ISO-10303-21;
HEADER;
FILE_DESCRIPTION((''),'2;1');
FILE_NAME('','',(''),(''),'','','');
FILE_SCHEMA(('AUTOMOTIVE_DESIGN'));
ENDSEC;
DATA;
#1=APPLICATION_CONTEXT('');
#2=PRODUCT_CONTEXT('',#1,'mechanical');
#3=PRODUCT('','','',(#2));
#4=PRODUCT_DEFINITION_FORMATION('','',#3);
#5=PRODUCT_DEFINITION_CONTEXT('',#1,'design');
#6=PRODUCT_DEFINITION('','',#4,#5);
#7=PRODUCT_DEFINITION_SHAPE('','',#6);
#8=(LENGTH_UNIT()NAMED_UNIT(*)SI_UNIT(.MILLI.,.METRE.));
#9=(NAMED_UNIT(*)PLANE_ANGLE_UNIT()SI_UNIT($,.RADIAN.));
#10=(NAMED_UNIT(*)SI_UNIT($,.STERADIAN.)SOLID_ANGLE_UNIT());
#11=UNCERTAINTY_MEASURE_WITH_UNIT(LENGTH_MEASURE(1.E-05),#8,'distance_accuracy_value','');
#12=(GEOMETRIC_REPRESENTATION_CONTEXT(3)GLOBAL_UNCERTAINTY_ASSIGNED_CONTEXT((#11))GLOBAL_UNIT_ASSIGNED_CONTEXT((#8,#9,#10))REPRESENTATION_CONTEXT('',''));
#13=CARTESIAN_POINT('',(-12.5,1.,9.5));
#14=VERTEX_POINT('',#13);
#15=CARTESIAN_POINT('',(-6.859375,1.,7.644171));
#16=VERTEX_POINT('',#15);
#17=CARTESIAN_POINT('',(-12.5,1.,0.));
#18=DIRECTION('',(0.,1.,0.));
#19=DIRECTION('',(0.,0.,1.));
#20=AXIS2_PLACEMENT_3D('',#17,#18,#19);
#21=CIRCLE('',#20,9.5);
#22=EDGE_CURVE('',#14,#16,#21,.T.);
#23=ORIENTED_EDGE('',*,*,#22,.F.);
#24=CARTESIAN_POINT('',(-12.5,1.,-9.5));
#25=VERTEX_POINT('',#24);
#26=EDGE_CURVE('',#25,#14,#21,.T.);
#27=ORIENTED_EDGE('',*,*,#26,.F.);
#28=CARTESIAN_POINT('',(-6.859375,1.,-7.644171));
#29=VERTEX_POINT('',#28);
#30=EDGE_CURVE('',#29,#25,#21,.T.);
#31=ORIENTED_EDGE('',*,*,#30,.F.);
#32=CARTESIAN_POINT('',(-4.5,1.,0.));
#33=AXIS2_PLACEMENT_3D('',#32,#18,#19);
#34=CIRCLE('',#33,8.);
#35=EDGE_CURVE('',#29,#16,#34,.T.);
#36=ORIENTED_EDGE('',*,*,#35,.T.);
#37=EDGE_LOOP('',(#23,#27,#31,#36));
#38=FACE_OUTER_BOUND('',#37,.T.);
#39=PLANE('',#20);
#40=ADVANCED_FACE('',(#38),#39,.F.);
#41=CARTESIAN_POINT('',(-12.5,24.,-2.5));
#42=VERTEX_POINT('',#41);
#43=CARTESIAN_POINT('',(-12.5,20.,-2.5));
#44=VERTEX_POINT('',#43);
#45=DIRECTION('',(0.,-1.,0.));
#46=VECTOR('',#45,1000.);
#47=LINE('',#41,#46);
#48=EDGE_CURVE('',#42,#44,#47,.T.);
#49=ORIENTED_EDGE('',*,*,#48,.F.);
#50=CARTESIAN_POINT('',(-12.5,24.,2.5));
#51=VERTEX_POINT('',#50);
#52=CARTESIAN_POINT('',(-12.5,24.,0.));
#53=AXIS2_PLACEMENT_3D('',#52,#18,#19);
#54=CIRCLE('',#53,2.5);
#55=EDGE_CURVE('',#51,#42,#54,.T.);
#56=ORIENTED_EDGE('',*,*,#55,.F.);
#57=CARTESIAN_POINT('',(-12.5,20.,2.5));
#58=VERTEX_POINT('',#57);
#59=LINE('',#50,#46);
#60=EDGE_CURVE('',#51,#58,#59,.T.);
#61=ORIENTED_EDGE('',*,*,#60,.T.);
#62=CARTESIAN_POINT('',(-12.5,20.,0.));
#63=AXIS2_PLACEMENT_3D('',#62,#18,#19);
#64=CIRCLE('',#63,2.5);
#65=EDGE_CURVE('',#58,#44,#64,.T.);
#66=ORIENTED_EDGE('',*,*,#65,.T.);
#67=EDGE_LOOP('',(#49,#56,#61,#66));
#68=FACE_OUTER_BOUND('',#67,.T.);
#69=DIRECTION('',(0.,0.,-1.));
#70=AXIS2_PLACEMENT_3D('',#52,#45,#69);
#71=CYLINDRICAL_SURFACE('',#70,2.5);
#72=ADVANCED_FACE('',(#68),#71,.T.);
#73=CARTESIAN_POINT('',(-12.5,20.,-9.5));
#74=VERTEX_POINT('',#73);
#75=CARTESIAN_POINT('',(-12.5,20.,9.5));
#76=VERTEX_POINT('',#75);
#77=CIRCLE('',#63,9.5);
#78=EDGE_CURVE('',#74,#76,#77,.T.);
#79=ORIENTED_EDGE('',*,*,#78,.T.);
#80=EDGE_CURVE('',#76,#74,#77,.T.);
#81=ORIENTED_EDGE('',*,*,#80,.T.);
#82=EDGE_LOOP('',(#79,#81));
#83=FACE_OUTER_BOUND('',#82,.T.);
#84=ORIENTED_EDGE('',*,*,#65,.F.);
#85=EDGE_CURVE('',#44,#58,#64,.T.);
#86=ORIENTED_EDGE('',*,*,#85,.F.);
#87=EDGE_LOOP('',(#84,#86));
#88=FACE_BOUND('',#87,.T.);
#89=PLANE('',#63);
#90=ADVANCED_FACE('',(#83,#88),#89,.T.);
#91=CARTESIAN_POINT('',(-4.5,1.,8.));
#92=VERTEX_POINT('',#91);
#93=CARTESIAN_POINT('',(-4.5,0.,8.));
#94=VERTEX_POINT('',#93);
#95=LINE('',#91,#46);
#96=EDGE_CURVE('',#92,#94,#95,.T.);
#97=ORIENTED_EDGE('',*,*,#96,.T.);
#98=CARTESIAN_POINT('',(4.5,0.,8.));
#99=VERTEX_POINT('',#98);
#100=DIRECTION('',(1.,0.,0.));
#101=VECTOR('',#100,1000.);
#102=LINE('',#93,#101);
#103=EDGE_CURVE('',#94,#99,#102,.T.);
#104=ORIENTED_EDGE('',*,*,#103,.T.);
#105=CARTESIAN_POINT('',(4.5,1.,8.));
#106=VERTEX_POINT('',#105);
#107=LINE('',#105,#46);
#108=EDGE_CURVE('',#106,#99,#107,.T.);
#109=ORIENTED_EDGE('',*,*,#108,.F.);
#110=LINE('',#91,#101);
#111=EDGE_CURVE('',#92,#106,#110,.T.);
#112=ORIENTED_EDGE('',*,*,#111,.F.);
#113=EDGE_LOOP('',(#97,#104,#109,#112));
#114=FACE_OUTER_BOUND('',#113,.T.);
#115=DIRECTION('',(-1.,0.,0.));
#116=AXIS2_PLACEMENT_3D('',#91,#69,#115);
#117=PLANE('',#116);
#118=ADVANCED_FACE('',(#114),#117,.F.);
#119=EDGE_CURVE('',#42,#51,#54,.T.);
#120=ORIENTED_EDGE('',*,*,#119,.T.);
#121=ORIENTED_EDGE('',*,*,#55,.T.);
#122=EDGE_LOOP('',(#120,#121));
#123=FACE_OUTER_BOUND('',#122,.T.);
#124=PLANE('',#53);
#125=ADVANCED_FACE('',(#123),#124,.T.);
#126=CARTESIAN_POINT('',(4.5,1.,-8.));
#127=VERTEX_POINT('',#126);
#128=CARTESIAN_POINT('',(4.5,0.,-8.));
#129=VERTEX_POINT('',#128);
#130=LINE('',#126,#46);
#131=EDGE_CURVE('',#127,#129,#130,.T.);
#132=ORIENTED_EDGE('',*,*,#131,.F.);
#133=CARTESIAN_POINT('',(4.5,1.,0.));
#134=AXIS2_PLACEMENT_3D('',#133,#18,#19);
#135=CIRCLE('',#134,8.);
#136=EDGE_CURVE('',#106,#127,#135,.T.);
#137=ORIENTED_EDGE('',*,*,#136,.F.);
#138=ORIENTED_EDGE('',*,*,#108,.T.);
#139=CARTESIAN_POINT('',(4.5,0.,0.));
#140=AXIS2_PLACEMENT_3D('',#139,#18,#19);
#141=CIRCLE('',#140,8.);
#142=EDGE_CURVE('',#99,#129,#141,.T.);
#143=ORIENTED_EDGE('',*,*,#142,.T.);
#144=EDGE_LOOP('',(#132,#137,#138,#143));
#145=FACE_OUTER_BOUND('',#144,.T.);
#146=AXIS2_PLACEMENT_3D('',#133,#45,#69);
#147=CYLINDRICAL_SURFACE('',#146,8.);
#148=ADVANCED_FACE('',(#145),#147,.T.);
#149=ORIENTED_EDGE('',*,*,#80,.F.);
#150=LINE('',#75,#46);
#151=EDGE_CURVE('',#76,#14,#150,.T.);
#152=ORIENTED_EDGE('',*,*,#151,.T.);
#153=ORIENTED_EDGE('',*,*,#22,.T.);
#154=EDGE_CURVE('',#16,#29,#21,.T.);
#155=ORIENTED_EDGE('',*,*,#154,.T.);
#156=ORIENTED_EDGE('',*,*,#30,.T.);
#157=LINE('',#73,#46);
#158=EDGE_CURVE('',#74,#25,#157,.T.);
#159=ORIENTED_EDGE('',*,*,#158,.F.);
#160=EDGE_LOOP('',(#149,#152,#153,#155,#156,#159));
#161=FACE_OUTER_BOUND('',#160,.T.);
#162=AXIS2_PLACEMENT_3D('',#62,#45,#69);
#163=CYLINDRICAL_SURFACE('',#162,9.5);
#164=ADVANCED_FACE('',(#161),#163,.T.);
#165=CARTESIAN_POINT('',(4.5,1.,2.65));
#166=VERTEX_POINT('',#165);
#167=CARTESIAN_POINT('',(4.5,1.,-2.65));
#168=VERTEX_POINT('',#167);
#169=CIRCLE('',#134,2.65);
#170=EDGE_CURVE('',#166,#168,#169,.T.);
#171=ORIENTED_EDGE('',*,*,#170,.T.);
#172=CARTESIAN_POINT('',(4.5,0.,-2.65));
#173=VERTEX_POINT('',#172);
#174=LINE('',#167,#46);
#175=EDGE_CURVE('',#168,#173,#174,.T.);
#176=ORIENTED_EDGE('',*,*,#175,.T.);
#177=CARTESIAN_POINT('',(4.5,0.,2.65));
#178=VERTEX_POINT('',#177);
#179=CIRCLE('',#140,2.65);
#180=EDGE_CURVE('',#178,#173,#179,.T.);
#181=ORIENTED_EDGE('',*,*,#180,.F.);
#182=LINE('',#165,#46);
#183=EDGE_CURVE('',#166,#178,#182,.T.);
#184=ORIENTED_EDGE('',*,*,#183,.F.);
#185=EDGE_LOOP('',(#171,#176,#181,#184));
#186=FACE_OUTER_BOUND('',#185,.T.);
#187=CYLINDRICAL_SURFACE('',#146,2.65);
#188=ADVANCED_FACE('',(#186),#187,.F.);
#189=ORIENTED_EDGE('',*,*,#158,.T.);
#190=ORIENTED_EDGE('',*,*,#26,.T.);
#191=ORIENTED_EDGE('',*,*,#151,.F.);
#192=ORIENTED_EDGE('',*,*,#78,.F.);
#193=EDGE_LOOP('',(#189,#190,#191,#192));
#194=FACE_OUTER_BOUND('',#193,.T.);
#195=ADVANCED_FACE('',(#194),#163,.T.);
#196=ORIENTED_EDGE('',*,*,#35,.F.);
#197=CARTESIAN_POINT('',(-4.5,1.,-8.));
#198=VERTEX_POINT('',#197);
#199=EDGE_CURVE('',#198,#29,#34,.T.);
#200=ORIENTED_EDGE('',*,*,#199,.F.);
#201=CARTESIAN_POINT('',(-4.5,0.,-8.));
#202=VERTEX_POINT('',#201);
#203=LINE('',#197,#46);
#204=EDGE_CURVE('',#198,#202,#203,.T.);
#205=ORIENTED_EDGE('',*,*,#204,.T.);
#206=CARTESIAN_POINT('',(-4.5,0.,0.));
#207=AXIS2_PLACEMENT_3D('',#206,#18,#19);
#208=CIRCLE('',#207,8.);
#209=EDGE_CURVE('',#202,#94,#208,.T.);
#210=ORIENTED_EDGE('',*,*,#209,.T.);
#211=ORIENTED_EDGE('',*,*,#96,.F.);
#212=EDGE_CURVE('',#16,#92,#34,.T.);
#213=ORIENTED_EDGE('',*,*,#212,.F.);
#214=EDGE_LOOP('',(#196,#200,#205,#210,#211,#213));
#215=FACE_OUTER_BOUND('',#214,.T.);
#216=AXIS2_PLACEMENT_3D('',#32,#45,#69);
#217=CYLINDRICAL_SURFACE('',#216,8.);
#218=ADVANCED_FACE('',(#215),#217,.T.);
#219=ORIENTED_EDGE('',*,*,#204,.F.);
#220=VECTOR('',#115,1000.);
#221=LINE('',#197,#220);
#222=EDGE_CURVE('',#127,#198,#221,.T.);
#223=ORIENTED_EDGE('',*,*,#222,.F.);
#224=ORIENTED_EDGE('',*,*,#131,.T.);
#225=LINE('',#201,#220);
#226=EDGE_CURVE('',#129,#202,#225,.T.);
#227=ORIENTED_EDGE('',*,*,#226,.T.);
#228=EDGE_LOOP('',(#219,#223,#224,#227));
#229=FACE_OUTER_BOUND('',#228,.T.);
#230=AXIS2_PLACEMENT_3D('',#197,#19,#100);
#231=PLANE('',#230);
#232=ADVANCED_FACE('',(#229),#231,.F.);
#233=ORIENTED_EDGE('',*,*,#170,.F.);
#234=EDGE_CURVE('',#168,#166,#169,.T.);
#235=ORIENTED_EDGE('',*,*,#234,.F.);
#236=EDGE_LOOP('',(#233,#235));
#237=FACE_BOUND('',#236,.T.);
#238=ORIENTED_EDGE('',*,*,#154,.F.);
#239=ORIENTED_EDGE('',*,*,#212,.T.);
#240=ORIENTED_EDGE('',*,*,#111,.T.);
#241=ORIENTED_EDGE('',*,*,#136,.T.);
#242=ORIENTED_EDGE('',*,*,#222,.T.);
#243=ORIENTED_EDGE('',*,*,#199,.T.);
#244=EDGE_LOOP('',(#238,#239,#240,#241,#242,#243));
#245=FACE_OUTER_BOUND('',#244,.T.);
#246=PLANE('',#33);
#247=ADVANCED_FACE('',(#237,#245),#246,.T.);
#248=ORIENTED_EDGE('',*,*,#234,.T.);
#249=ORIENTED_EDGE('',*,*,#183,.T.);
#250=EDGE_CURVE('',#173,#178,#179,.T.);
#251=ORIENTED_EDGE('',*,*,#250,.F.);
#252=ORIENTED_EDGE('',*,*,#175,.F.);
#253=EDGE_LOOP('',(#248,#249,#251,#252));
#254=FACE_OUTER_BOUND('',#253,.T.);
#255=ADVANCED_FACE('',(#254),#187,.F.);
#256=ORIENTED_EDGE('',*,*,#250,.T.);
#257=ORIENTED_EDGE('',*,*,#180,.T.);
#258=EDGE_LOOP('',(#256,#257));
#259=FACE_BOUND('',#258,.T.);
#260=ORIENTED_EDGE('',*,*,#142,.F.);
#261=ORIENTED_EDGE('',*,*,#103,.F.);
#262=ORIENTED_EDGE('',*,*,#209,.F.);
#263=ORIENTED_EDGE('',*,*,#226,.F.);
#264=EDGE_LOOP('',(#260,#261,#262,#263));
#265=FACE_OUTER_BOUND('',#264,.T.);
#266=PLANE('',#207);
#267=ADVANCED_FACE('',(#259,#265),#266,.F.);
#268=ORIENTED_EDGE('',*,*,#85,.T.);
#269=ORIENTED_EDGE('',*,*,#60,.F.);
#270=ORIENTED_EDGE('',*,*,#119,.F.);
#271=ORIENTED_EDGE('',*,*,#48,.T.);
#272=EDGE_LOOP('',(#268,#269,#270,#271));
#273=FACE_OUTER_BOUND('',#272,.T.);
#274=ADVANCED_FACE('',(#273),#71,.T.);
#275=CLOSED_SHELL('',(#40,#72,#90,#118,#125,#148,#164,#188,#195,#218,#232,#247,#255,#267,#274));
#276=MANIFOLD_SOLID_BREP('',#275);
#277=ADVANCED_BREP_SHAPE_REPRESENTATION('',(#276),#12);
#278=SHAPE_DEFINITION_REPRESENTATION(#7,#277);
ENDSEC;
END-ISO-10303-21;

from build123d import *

# Parameters (mm, degrees)
MOUNTING_TAB_PROFILE_R               = 2.65
MOUNTING_TAB_1MM_WITH_HOLE_5_3_DEPTH = 1
CHAMBER_BODY_PROFILE_19_R            = 9.5
CHAMBER_BODY_19X19_DEPTH             = 19
TOP_PIN_PROFILE_5_R                  = 2.5
TOP_PIN_5X4_DEPTH                    = 4


with BuildPart() as part:
    # Mounting Tab Profile → Mounting Tab 1mm with Hole Ø5.3 (new body)
    with BuildSketch(Plane(origin=(0, 0, 0), x_dir=(1, 0, 0), z_dir=(0, 1, 0))):
        with BuildLine():
            Line((-4.5, 8), (4.5, 8))
            ThreePointArc((4.5, 8), (12.5, 0), (4.5, -8))
            Line((4.5, -8), (-4.5, -8))
            ThreePointArc((-4.5, -8), (-12.5, 0), (-4.5, 8))
        make_face()
        with Locations(Location((4.5, 0, 0), (0, 0, 270))):
            Circle(MOUNTING_TAB_PROFILE_R, mode=Mode.SUBTRACT)
    extrude(amount=MOUNTING_TAB_1MM_WITH_HOLE_5_3_DEPTH)

    # Chamber Body Profile Ø19 → Chamber Body Ø19x19 (add)
    with BuildSketch(Plane(origin=(0, 1, 0), x_dir=(1, 0, 0), z_dir=(0, 1, 0))):
        with Locations(Location((-12.5, 0, 0), (0, 0, 53.576426358))):
            Circle(CHAMBER_BODY_PROFILE_19_R)
    extrude(amount=CHAMBER_BODY_19X19_DEPTH)

    # Top Pin Profile Ø5 → Top Pin Ø5x4 (add)
    with BuildSketch(Plane(origin=(0, 20, 0), x_dir=(1, 0, 0), z_dir=(0, 1, 0))):
        with Locations(Location((-12.5, 0, 0), (0, 0, 270))):
            Circle(TOP_PIN_PROFILE_5_R)
    extrude(amount=TOP_PIN_5X4_DEPTH)


solid = part.part
